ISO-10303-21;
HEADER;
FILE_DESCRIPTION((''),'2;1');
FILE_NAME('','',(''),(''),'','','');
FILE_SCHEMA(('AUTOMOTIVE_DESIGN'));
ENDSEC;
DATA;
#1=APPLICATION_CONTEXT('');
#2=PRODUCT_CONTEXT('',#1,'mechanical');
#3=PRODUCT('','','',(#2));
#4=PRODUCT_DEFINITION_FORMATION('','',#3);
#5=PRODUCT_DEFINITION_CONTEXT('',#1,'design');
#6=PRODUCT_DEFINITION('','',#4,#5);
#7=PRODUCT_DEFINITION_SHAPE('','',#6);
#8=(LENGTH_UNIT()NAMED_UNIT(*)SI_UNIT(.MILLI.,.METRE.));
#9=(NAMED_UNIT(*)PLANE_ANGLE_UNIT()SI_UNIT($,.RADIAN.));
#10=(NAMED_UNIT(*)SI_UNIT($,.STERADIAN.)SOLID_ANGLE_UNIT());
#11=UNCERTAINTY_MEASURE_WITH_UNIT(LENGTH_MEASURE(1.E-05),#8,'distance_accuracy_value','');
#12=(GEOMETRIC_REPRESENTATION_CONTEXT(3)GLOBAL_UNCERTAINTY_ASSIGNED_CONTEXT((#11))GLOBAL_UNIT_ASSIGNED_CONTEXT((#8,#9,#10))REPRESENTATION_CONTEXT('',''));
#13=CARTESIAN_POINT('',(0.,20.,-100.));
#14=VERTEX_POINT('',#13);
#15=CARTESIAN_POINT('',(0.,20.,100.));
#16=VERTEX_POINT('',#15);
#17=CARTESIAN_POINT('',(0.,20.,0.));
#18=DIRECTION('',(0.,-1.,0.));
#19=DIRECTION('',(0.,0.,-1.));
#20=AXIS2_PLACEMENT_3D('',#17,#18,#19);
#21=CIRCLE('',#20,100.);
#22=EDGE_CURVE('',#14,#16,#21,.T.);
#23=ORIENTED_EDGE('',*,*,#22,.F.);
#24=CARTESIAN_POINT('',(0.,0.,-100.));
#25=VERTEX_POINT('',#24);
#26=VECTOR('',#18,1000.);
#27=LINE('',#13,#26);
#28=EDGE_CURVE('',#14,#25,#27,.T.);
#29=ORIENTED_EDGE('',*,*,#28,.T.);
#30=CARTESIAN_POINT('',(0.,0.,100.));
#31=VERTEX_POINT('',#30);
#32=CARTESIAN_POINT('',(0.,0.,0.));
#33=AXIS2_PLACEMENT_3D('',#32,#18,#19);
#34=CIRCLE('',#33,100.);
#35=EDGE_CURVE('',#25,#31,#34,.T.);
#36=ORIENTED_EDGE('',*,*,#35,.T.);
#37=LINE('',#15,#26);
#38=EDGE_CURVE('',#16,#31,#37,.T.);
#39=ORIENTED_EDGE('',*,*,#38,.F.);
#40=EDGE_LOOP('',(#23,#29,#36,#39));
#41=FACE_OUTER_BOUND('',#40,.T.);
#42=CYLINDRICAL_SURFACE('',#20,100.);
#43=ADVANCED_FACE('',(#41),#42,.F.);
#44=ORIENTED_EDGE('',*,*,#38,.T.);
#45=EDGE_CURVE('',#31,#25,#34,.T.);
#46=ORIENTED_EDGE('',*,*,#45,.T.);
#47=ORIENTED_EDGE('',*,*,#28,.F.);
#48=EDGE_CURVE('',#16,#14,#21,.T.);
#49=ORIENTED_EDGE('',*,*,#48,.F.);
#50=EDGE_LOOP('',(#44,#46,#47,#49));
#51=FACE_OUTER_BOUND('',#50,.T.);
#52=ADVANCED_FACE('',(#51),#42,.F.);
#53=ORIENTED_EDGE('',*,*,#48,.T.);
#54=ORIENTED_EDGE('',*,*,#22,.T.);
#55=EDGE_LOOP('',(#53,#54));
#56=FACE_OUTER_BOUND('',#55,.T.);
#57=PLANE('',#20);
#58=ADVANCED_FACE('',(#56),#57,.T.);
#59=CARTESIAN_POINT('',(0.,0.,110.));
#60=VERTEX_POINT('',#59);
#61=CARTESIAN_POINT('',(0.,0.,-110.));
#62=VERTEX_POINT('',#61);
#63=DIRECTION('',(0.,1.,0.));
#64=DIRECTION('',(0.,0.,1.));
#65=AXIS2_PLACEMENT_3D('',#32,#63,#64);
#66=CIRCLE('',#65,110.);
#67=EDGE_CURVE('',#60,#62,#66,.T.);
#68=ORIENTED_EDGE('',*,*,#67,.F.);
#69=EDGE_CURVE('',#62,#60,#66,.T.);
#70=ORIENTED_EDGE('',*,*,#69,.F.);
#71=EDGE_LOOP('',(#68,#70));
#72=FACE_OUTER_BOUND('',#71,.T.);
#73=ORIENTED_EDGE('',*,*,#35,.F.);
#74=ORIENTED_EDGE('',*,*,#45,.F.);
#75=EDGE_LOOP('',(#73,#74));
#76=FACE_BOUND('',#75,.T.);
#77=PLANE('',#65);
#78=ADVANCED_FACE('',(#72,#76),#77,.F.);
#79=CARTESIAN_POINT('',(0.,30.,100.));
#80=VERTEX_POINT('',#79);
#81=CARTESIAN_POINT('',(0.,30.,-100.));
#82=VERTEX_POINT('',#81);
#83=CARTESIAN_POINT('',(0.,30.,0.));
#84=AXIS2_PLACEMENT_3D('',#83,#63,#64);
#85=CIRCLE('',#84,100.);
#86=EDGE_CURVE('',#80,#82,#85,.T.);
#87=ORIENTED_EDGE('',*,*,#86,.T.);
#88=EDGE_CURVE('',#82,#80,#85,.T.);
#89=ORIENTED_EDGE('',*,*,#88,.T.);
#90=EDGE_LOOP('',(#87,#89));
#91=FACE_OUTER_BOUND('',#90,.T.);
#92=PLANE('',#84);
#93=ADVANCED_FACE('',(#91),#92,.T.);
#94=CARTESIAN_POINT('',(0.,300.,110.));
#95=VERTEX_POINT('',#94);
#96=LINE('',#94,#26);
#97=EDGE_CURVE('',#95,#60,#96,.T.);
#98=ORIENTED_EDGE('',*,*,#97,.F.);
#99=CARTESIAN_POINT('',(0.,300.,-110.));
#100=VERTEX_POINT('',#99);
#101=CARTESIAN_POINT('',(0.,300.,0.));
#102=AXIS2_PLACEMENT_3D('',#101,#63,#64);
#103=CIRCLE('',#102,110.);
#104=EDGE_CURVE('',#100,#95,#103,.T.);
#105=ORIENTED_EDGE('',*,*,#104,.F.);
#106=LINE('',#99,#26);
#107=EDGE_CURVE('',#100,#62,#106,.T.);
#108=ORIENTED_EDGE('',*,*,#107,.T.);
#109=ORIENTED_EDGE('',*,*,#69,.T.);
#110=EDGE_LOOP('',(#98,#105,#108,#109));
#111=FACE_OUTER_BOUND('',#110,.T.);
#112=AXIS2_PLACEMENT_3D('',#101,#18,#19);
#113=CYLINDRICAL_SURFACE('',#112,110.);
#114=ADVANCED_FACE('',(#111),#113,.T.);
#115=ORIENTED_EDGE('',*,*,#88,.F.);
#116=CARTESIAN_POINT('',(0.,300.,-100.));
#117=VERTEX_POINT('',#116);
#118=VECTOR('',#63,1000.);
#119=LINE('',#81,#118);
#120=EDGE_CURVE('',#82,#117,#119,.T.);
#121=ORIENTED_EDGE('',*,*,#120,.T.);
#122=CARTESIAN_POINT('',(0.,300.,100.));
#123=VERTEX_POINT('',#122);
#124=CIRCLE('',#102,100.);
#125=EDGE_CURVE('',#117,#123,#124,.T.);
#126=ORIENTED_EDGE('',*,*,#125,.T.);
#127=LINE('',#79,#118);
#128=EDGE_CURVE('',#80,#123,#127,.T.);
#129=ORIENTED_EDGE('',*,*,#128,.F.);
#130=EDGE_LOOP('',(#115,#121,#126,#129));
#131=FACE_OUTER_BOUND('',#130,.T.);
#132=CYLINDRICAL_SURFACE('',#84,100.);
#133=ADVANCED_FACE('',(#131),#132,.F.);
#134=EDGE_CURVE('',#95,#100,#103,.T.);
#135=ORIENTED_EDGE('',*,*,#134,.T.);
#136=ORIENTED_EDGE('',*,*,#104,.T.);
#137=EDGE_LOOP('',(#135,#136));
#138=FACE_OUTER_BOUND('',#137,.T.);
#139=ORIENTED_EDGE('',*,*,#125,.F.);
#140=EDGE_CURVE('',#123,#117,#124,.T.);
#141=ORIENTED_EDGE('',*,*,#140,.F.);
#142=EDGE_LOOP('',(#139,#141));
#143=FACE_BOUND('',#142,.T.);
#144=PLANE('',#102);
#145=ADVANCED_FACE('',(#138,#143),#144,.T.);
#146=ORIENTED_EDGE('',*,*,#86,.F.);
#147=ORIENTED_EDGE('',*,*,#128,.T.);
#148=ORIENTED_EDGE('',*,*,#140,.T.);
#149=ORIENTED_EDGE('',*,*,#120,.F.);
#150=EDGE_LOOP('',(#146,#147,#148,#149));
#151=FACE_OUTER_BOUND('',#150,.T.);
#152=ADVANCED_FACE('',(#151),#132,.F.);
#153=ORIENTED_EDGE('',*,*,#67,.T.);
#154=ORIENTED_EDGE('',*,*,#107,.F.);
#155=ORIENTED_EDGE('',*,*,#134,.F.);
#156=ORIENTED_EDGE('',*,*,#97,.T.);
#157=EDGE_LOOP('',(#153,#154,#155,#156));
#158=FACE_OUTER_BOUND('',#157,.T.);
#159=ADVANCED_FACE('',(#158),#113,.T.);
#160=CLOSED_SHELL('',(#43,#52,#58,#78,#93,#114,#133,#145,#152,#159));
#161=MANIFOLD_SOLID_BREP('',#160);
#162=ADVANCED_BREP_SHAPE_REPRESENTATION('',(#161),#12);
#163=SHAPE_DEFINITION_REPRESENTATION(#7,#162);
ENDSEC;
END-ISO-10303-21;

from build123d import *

# Parameters (mm, degrees)
SKETCH1_R           = 110
BOSS_EXTRUDE1_DEPTH = 300
SKETCH3_R           = 100
CUT_EXTRUDE1_DEPTH  = 20
CUT_EXTRUDE2_START  = -270
SKETCH4_R           = 100
CUT_EXTRUDE2_DEPTH  = 270


with BuildPart() as part:
    # Sketch1 → Boss-Extrude1 (new body)
    with BuildSketch(Plane(origin=(0, 0, 0), x_dir=(1, 0, 0), z_dir=(0, 1, 0))):
        with Locations(Location((0, 0, 0), (0, 0, 270))):
            Circle(SKETCH1_R)
    extrude(amount=BOSS_EXTRUDE1_DEPTH)

    # Sketch3 → Cut-Extrude1 (cut)
    with BuildSketch(Plane.XZ):
        with Locations(Location((0, 0, 0), (0, 0, 270))):
            Circle(SKETCH3_R)
    extrude(amount=-CUT_EXTRUDE1_DEPTH, mode=Mode.SUBTRACT)

    # Sketch4 → Cut-Extrude2 (cut)
    with BuildSketch(Plane(origin=(0, 300, 0), x_dir=(1, 0, 0), z_dir=(0, 1, 0)).offset(CUT_EXTRUDE2_START)):
        with Locations(Location((0, 0, 0), (0, 0, 90))):
            Circle(SKETCH4_R)
    extrude(amount=CUT_EXTRUDE2_DEPTH, mode=Mode.SUBTRACT)


solid = part.part
